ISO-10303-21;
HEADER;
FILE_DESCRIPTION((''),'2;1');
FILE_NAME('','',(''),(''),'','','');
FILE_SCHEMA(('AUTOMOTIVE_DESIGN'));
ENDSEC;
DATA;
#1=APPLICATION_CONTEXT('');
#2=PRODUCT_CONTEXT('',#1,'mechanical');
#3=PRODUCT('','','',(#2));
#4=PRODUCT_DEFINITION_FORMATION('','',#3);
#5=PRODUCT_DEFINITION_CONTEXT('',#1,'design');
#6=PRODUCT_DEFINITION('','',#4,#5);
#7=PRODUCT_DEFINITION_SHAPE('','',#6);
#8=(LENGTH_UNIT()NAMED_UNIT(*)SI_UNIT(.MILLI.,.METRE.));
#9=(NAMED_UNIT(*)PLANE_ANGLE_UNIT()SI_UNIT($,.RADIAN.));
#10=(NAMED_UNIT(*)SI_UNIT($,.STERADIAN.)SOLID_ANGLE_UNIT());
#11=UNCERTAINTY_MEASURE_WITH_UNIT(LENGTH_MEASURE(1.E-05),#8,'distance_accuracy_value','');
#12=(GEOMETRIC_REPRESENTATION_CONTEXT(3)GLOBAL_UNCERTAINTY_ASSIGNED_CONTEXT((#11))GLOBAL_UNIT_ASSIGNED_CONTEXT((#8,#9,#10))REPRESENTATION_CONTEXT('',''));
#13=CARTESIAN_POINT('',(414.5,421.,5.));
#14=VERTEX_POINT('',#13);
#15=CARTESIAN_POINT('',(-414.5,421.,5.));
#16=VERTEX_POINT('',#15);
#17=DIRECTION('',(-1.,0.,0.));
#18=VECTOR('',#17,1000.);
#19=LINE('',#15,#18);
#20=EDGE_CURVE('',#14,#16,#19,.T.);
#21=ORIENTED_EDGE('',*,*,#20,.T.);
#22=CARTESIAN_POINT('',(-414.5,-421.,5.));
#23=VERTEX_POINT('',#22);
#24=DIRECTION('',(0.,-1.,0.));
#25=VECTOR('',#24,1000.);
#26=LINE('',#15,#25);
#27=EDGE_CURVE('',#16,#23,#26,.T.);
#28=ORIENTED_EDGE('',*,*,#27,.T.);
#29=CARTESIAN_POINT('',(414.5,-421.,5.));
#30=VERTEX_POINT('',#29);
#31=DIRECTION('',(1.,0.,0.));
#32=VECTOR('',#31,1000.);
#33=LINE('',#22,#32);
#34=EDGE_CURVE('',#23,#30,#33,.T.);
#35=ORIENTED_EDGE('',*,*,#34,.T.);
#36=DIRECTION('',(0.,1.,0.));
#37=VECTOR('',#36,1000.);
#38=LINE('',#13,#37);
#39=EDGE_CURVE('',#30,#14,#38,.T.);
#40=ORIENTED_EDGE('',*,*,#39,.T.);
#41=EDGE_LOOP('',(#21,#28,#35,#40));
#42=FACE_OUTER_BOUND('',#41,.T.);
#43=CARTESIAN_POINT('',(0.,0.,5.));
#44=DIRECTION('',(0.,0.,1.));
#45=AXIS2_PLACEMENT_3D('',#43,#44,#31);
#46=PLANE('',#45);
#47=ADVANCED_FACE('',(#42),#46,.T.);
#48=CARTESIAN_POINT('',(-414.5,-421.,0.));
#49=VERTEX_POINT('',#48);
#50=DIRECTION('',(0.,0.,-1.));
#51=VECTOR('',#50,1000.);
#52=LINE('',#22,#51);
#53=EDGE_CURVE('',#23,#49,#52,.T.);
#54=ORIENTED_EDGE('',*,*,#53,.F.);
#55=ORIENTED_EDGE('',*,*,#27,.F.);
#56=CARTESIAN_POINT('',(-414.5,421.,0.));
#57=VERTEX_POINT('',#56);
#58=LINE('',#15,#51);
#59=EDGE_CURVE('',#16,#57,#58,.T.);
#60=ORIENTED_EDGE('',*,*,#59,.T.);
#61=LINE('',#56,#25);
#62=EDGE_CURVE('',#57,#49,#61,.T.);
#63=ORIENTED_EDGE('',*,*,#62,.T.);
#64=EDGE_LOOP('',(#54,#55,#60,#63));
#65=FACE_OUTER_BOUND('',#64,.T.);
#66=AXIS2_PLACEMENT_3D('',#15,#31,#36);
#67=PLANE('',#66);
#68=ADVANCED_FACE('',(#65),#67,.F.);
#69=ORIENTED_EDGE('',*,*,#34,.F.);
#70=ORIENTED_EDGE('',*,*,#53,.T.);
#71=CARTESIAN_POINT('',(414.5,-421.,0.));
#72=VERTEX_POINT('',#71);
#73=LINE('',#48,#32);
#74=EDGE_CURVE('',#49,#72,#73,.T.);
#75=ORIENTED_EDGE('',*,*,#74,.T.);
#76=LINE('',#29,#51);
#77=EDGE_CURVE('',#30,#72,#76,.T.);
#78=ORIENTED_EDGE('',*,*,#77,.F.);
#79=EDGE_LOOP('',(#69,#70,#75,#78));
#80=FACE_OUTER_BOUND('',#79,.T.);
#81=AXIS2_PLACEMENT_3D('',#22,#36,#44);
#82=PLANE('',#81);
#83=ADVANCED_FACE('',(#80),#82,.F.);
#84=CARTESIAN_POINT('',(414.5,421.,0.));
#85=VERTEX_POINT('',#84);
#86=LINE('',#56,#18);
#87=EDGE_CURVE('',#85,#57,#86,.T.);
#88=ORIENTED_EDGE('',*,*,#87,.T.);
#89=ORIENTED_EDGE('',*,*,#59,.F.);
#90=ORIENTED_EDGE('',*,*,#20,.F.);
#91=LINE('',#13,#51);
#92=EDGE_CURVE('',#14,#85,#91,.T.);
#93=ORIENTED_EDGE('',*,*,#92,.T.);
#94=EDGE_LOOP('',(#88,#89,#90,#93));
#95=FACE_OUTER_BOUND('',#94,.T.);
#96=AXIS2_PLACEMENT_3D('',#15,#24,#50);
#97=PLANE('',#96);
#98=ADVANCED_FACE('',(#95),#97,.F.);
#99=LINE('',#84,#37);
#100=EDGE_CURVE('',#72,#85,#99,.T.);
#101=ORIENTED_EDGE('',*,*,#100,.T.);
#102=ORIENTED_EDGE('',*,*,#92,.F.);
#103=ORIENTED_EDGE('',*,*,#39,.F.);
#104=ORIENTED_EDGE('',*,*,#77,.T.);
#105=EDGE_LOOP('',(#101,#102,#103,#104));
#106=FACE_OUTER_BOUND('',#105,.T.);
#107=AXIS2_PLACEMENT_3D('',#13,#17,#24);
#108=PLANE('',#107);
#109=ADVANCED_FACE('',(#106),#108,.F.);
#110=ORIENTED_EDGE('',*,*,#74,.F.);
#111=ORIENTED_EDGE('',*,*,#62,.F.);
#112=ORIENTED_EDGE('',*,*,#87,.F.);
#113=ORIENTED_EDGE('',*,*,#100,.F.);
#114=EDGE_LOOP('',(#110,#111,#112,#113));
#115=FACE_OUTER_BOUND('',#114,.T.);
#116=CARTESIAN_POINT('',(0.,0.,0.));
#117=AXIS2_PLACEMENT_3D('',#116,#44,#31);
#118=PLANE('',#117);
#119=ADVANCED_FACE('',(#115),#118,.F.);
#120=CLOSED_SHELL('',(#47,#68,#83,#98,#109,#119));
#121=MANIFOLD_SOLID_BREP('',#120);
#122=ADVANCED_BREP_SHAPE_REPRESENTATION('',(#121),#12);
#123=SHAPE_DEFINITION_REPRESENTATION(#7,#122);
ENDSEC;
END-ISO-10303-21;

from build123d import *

# Parameters (mm, degrees)
SKETCH_1_W      = 829
SKETCH_1_H      = 842
EXTRUDE_1_DEPTH = 5


with BuildPart() as part:
    # 草图1 → 凸台-拉伸1 (new body)
    with BuildSketch(Plane.XY):
        Rectangle(SKETCH_1_W, SKETCH_1_H)
    extrude(amount=EXTRUDE_1_DEPTH)


solid = part.part
